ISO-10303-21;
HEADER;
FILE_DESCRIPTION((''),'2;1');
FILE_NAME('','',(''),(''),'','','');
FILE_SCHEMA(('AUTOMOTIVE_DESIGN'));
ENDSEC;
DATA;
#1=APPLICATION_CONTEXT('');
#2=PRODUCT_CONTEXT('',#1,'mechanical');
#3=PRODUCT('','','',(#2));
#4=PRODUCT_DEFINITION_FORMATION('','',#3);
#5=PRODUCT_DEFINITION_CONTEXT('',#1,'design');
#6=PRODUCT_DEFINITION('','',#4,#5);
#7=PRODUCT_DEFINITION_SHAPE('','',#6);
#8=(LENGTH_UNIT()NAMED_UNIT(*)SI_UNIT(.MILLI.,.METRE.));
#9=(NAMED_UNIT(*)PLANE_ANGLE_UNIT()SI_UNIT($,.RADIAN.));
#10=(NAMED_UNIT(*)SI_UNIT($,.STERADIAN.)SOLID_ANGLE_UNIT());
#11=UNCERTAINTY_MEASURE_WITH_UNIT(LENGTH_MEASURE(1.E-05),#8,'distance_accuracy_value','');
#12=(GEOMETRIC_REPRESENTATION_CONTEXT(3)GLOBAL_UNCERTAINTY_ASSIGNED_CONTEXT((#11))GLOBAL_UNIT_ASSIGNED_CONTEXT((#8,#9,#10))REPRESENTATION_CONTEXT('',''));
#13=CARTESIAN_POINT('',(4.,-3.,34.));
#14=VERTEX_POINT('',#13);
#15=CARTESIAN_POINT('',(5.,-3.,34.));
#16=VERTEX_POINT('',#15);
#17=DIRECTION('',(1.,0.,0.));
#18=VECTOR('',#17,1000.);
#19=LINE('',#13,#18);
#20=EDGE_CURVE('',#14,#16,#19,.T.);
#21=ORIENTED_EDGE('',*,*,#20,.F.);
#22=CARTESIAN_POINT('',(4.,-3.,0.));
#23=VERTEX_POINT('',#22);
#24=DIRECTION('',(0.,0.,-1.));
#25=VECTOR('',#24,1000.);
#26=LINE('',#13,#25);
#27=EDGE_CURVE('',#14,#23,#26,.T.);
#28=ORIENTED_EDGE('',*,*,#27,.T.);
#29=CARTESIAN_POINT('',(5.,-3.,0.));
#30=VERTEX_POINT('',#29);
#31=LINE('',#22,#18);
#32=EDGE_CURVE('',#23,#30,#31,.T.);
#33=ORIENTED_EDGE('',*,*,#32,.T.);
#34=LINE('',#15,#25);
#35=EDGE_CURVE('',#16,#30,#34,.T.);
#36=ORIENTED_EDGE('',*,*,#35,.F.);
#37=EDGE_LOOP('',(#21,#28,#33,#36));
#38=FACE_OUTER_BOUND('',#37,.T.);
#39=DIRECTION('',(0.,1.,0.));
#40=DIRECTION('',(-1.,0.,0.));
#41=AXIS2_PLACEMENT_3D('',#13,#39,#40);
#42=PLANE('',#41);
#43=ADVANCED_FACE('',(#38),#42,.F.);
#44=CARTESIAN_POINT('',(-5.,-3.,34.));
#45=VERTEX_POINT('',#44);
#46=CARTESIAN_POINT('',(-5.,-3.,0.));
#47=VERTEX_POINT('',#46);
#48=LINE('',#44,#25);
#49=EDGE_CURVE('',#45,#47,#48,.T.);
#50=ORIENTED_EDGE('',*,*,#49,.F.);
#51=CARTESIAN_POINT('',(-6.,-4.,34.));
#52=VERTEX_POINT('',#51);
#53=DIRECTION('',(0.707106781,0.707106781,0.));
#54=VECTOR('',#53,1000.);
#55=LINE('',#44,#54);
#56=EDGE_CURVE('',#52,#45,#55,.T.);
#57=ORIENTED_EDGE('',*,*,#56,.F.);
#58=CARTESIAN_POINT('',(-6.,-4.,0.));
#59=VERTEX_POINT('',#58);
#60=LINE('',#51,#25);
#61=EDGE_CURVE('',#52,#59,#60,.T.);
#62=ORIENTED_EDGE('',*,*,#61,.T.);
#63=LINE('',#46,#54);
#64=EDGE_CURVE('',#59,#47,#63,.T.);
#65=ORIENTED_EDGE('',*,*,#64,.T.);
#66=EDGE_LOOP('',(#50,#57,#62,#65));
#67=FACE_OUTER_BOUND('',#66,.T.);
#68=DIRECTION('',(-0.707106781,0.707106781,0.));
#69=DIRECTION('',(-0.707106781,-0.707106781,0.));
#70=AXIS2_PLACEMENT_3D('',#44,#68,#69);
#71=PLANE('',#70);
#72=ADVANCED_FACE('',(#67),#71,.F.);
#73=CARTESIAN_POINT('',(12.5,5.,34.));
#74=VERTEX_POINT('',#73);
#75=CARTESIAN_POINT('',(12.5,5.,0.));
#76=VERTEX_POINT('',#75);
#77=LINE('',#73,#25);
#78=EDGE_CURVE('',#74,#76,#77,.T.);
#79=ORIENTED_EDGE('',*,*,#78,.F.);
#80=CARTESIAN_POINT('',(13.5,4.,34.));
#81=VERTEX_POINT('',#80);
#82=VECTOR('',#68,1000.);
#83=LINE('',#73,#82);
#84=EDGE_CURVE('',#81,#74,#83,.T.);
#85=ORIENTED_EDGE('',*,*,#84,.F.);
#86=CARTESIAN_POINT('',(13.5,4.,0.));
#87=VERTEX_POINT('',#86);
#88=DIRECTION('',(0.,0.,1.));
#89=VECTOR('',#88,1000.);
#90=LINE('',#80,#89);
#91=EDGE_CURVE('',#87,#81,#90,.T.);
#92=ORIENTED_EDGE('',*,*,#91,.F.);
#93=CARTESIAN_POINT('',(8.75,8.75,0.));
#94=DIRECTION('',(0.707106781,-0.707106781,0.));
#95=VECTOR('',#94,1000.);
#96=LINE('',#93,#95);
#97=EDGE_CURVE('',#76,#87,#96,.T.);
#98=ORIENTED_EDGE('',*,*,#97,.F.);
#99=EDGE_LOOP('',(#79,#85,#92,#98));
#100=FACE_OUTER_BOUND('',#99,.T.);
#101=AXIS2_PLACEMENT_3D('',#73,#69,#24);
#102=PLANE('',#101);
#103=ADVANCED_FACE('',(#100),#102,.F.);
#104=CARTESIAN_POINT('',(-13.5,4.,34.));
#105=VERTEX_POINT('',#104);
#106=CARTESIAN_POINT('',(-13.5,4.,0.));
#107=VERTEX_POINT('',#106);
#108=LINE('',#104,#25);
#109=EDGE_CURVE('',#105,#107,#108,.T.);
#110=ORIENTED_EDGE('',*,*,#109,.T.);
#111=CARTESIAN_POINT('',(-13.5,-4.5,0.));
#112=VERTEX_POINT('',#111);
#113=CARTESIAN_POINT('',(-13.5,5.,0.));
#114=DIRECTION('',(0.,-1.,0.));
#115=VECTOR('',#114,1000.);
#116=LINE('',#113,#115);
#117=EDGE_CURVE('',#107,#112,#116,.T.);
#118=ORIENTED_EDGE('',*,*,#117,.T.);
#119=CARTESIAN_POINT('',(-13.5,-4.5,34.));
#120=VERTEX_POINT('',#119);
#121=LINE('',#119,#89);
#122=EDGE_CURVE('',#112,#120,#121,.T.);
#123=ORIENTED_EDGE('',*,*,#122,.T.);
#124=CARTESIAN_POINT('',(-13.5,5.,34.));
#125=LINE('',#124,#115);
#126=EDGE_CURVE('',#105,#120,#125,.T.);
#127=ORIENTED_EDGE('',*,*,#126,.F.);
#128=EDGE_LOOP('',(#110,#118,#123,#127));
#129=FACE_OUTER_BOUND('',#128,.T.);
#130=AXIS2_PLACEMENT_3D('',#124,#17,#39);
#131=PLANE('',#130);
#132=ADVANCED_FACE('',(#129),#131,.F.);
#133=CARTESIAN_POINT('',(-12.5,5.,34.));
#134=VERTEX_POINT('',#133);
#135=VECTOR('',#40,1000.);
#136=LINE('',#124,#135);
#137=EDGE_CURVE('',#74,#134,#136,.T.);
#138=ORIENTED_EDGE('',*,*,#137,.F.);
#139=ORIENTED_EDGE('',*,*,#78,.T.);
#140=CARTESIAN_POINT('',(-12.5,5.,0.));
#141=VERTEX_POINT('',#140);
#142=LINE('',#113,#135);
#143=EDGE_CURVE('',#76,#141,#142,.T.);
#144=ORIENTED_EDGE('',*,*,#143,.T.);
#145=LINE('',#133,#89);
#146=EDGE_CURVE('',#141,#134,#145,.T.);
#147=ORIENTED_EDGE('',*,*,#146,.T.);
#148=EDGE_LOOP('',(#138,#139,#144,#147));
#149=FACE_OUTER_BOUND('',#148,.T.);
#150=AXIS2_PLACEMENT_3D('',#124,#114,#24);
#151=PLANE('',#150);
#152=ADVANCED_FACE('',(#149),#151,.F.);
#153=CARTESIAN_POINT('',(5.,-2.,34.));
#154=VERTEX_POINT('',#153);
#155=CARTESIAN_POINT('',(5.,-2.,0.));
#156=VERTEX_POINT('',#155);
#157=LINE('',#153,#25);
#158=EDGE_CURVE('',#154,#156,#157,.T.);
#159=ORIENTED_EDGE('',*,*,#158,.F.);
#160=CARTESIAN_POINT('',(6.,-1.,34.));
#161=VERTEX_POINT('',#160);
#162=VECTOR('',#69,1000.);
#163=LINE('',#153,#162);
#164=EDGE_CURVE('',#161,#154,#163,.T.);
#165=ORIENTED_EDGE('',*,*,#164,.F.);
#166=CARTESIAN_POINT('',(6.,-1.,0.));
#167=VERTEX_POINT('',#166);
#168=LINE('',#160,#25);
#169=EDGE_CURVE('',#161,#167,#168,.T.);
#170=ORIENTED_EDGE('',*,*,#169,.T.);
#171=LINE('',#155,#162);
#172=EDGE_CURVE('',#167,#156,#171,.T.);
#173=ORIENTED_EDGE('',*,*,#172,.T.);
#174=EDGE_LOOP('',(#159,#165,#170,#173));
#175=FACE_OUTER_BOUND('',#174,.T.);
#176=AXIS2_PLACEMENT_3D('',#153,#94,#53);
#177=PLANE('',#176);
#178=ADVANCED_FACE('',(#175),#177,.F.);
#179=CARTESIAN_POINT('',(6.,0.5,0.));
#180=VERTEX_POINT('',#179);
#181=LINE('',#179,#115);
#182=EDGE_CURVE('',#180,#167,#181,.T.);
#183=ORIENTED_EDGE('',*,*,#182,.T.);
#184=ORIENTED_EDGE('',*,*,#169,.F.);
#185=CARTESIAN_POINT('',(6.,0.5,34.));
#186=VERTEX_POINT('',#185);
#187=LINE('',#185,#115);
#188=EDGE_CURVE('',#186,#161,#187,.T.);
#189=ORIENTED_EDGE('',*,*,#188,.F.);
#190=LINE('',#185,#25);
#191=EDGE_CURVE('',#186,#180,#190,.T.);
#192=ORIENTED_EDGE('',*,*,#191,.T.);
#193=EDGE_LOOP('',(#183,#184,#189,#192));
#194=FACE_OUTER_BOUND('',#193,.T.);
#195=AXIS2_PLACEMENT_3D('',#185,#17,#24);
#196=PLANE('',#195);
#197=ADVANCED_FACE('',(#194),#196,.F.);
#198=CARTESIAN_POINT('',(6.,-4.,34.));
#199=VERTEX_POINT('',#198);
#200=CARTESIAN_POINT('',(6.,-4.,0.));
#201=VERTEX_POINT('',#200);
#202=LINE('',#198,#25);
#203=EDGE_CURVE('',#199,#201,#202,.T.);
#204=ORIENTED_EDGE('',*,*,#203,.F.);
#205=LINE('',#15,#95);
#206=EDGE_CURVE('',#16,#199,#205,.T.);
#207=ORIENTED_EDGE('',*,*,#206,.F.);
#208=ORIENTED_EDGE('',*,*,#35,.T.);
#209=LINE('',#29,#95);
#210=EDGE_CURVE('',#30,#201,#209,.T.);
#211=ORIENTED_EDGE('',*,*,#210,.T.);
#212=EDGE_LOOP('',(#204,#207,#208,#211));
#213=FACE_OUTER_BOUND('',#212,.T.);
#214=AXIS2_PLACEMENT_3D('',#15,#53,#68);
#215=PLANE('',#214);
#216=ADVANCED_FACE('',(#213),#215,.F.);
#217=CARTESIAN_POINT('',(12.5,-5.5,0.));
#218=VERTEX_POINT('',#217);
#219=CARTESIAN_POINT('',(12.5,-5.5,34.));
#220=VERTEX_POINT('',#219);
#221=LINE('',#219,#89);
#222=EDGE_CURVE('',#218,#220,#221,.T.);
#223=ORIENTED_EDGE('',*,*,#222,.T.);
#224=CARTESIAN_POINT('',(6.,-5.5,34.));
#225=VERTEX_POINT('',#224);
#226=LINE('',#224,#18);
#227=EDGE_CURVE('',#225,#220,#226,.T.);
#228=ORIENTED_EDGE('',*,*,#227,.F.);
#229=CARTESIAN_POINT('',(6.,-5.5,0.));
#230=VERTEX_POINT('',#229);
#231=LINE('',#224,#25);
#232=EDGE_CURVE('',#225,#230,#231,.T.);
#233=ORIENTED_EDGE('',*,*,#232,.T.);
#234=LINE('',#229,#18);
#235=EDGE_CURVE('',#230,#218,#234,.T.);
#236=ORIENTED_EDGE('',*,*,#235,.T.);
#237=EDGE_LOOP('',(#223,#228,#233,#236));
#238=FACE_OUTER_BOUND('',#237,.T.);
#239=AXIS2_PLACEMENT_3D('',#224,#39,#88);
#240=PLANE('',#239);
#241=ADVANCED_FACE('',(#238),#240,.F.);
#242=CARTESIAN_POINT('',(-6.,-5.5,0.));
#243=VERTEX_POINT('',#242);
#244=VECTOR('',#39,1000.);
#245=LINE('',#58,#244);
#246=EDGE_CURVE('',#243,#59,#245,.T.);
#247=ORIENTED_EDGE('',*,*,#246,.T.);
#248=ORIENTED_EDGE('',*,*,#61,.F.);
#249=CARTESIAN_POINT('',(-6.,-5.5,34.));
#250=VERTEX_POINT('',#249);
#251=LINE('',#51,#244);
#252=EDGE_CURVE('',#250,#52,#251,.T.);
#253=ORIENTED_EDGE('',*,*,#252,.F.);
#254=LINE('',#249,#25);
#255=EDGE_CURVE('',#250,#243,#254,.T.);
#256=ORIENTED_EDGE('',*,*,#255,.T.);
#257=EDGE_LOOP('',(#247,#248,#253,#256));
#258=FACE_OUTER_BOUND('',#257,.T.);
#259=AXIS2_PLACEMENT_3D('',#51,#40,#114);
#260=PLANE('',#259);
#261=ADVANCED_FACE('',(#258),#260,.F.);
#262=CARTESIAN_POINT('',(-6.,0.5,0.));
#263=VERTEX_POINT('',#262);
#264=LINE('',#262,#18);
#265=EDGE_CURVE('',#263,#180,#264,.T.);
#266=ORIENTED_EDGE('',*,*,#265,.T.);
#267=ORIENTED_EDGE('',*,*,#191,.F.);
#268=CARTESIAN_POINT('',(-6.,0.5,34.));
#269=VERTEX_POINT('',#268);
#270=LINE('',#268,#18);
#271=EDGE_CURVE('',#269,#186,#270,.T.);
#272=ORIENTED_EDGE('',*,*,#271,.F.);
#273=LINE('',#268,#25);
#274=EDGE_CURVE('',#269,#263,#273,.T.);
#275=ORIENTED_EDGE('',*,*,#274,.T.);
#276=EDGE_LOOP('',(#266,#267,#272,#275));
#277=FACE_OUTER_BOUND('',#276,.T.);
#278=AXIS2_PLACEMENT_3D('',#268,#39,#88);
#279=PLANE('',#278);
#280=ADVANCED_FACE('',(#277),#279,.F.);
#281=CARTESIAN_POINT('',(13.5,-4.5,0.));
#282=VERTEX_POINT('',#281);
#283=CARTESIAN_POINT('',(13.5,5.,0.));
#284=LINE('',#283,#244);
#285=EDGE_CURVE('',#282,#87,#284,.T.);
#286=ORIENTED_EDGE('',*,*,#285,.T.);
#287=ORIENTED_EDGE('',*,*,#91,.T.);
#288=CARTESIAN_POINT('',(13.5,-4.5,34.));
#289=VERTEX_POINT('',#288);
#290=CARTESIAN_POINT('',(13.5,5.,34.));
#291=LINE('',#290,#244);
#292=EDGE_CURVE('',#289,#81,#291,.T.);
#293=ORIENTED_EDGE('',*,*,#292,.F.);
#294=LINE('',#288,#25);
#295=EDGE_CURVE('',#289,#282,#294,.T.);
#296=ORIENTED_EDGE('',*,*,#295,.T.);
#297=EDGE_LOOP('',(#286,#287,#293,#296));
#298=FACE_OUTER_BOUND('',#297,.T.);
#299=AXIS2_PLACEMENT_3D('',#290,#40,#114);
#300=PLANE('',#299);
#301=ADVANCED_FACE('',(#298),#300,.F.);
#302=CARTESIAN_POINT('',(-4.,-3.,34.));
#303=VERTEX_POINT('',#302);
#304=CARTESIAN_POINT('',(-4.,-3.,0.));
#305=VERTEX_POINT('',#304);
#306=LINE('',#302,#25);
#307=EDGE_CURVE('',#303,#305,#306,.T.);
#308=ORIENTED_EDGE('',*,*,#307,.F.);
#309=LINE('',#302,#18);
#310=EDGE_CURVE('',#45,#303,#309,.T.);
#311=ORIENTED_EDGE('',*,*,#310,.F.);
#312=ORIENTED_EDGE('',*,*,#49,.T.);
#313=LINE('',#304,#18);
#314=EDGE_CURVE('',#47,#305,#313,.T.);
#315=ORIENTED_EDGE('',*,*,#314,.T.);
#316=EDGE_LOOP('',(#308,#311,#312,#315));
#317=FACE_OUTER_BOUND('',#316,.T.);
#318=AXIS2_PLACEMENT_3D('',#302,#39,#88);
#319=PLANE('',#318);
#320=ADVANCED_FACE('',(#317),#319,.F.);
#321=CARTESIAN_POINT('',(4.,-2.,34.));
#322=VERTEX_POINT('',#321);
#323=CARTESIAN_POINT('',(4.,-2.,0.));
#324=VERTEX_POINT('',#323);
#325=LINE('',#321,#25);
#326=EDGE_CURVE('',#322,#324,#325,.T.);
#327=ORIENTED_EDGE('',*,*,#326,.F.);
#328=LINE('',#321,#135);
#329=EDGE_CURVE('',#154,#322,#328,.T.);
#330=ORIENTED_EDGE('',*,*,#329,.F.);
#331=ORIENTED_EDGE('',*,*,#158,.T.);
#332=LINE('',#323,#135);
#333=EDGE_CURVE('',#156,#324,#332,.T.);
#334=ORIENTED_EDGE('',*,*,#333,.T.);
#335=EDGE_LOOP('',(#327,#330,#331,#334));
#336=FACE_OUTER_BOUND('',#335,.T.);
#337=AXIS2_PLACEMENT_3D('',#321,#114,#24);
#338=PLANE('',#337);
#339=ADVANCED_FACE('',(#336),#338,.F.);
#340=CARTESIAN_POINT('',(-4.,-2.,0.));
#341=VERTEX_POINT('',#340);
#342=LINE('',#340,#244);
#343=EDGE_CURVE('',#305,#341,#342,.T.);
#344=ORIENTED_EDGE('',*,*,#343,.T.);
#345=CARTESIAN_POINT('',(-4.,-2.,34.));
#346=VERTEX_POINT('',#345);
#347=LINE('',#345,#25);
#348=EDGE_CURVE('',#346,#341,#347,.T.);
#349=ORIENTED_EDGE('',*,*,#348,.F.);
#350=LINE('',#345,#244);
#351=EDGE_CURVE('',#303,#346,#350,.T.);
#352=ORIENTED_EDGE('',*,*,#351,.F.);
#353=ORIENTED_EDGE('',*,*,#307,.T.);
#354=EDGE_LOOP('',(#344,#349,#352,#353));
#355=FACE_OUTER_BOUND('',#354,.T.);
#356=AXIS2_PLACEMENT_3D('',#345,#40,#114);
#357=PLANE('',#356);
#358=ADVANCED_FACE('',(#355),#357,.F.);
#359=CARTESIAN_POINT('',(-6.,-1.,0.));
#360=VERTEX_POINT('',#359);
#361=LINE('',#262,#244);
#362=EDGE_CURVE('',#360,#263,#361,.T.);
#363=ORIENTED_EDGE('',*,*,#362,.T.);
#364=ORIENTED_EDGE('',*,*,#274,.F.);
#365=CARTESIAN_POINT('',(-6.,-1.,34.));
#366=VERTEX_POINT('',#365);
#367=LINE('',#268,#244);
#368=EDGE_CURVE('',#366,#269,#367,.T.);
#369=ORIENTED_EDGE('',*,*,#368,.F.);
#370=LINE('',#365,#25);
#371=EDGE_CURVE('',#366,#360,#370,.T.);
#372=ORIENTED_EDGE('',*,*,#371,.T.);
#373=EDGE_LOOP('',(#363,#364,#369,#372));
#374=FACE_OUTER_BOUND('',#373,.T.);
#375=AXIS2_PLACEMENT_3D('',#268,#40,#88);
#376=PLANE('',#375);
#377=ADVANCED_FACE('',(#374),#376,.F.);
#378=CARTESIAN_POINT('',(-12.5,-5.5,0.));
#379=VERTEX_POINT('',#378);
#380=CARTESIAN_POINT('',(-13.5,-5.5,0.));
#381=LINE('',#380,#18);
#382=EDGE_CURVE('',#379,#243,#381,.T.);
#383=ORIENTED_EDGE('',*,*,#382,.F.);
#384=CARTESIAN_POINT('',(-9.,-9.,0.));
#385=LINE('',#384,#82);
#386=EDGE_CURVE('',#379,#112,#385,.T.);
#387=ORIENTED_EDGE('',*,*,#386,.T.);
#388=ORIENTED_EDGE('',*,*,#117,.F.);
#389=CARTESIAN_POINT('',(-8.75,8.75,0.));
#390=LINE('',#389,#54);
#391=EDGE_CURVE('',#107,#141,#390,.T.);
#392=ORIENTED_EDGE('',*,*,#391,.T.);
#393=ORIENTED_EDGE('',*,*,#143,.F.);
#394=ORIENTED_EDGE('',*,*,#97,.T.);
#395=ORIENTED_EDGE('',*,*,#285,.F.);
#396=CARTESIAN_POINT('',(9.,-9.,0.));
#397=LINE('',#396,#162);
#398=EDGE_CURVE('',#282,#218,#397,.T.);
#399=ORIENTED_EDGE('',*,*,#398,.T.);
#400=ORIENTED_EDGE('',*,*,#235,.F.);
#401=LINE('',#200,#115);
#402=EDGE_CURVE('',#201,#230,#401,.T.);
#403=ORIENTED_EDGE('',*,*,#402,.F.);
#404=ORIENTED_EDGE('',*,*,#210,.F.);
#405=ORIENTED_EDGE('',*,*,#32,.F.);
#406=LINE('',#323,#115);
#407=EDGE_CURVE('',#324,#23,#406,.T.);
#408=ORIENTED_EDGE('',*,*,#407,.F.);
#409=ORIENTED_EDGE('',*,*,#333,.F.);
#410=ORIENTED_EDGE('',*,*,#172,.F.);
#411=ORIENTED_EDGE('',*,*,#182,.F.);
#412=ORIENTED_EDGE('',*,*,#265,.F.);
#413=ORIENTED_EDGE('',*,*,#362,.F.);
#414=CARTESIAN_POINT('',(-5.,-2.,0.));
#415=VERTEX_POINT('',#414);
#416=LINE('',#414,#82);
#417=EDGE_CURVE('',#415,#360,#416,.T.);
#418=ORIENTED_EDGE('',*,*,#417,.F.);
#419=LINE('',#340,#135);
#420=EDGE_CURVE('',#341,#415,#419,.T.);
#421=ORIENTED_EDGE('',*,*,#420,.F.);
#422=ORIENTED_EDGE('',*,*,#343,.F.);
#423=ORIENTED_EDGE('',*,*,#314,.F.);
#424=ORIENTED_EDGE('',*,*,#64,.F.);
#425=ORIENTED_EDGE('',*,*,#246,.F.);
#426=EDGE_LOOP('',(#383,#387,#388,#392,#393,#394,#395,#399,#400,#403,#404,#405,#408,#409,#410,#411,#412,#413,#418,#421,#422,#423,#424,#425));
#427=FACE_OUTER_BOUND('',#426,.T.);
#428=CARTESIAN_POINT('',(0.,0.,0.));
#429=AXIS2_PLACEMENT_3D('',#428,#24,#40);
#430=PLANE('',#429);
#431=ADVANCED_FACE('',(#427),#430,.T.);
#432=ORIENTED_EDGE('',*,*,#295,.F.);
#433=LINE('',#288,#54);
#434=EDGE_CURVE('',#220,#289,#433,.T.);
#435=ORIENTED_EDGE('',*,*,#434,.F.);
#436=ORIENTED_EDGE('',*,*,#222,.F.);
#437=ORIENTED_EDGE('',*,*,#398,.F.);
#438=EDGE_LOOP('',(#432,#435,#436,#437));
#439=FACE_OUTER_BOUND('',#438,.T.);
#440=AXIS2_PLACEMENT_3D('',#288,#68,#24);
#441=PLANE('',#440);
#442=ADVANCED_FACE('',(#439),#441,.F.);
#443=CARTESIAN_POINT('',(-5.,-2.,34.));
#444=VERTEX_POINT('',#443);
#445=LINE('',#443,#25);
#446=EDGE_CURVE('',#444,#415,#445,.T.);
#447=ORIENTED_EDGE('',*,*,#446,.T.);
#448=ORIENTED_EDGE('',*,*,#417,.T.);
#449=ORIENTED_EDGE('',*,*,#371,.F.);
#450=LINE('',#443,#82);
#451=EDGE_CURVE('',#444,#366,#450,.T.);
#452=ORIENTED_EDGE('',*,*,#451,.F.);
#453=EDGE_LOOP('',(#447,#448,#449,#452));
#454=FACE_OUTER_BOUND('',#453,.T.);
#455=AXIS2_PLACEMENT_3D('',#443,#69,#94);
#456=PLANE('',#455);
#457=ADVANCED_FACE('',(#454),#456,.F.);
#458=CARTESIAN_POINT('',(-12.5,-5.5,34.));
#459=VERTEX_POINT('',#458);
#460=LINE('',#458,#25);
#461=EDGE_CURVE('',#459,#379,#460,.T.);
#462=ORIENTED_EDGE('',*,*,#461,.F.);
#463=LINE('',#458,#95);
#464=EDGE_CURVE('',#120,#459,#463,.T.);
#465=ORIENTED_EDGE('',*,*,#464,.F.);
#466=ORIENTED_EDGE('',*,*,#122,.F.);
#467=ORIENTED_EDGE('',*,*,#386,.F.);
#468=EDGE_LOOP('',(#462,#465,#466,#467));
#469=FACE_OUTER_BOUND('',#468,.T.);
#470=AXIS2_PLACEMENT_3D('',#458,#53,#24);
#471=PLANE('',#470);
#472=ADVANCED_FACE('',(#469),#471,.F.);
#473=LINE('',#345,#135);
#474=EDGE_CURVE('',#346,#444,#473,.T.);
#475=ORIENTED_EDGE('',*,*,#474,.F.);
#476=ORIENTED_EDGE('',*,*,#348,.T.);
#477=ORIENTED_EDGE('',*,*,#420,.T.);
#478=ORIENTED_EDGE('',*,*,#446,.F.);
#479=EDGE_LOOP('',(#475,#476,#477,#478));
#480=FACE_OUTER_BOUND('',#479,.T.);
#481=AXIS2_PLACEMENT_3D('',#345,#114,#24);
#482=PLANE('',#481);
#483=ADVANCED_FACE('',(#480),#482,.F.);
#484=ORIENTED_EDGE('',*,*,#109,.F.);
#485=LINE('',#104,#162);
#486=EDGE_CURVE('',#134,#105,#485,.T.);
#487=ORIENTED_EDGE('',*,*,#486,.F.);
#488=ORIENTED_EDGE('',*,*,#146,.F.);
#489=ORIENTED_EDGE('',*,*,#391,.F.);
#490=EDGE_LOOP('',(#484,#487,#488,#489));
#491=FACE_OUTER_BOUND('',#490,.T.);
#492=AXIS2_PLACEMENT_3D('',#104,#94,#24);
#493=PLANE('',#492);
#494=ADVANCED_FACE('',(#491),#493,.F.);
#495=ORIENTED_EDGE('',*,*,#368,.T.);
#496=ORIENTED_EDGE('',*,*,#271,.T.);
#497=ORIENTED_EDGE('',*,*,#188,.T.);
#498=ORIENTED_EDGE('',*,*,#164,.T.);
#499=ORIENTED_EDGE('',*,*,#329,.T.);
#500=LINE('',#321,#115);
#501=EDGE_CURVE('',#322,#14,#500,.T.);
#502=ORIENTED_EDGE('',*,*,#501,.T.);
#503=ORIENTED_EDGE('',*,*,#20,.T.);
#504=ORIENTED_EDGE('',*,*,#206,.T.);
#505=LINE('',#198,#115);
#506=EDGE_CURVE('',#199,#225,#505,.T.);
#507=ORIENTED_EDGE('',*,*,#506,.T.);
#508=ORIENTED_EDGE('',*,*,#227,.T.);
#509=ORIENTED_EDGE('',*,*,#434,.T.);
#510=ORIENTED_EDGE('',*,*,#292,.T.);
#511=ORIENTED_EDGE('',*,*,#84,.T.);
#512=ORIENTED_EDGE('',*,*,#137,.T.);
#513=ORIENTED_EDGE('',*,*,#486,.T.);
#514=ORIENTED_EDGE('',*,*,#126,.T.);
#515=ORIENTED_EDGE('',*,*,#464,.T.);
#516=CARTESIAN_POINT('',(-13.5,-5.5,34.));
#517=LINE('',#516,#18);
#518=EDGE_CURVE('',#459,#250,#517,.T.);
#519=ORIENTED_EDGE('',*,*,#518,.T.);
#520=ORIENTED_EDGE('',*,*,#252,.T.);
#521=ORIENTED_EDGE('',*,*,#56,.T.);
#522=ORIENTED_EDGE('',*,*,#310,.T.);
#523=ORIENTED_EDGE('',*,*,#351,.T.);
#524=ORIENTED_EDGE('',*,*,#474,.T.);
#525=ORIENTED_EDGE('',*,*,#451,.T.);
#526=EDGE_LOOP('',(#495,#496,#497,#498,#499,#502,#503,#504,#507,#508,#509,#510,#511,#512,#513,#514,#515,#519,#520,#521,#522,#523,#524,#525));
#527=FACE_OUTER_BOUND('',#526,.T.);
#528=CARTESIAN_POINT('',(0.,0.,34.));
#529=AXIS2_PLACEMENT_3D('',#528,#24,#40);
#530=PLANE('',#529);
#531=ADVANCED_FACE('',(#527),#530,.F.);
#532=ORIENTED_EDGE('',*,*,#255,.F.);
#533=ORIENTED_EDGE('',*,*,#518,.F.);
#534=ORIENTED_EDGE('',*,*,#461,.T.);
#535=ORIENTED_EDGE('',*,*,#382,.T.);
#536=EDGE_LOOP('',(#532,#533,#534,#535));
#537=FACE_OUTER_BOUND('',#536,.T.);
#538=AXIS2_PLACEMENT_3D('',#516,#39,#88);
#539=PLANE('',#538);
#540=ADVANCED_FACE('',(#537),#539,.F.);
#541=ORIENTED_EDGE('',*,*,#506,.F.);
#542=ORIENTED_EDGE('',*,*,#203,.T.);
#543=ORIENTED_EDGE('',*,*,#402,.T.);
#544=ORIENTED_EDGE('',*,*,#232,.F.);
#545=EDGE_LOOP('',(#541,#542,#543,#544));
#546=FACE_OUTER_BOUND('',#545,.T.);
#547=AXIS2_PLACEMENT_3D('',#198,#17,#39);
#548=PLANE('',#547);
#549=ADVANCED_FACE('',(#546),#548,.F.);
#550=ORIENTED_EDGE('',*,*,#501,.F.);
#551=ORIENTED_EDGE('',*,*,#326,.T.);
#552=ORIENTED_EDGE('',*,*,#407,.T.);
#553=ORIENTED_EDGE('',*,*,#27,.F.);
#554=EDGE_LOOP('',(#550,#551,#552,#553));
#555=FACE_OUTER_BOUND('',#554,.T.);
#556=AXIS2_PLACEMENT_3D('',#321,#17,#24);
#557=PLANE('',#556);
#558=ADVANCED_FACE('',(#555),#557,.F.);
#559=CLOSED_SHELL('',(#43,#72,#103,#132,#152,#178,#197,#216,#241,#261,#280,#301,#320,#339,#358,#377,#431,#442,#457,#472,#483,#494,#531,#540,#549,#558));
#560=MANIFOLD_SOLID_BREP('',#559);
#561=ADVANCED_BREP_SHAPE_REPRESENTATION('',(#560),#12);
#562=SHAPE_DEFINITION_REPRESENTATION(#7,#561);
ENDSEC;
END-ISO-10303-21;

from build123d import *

# Parameters (mm, degrees)
BOSS_EXTRUDE1_DEPTH = 34
CHAMFER1_SIZE       = 1


with BuildPart() as part:
    # Sketch1 → Boss-Extrude1 (new body)
    with BuildSketch(Plane.XY):
        Polygon((-13.5, 5), (13.5, 5), (13.5, -5.5), (6, -5.5), (6, -4), (5, -3), (4, -3), (4, -2), (5, -2), (6, -1), (6, 0.5), (-6, 0.5), (-6, -1), (-5, -2), (-4, -2), (-4, -3), (-5, -3), (-6, -4), (-6, -5.5), (-13.5, -5.5), align=None)
    extrude(amount=BOSS_EXTRUDE1_DEPTH)

    # Chamfer1
    chamfer1_edges = [part.edges().sort_by_distance(p)[0] for p in [
        (-13.5, -5.5, 17),
        (-13.5, 5, 17),
        (13.5, 5, 17),
        (13.5, -5.5, 17),
    ]]
    chamfer(chamfer1_edges, length=CHAMFER1_SIZE)


solid = part.part
